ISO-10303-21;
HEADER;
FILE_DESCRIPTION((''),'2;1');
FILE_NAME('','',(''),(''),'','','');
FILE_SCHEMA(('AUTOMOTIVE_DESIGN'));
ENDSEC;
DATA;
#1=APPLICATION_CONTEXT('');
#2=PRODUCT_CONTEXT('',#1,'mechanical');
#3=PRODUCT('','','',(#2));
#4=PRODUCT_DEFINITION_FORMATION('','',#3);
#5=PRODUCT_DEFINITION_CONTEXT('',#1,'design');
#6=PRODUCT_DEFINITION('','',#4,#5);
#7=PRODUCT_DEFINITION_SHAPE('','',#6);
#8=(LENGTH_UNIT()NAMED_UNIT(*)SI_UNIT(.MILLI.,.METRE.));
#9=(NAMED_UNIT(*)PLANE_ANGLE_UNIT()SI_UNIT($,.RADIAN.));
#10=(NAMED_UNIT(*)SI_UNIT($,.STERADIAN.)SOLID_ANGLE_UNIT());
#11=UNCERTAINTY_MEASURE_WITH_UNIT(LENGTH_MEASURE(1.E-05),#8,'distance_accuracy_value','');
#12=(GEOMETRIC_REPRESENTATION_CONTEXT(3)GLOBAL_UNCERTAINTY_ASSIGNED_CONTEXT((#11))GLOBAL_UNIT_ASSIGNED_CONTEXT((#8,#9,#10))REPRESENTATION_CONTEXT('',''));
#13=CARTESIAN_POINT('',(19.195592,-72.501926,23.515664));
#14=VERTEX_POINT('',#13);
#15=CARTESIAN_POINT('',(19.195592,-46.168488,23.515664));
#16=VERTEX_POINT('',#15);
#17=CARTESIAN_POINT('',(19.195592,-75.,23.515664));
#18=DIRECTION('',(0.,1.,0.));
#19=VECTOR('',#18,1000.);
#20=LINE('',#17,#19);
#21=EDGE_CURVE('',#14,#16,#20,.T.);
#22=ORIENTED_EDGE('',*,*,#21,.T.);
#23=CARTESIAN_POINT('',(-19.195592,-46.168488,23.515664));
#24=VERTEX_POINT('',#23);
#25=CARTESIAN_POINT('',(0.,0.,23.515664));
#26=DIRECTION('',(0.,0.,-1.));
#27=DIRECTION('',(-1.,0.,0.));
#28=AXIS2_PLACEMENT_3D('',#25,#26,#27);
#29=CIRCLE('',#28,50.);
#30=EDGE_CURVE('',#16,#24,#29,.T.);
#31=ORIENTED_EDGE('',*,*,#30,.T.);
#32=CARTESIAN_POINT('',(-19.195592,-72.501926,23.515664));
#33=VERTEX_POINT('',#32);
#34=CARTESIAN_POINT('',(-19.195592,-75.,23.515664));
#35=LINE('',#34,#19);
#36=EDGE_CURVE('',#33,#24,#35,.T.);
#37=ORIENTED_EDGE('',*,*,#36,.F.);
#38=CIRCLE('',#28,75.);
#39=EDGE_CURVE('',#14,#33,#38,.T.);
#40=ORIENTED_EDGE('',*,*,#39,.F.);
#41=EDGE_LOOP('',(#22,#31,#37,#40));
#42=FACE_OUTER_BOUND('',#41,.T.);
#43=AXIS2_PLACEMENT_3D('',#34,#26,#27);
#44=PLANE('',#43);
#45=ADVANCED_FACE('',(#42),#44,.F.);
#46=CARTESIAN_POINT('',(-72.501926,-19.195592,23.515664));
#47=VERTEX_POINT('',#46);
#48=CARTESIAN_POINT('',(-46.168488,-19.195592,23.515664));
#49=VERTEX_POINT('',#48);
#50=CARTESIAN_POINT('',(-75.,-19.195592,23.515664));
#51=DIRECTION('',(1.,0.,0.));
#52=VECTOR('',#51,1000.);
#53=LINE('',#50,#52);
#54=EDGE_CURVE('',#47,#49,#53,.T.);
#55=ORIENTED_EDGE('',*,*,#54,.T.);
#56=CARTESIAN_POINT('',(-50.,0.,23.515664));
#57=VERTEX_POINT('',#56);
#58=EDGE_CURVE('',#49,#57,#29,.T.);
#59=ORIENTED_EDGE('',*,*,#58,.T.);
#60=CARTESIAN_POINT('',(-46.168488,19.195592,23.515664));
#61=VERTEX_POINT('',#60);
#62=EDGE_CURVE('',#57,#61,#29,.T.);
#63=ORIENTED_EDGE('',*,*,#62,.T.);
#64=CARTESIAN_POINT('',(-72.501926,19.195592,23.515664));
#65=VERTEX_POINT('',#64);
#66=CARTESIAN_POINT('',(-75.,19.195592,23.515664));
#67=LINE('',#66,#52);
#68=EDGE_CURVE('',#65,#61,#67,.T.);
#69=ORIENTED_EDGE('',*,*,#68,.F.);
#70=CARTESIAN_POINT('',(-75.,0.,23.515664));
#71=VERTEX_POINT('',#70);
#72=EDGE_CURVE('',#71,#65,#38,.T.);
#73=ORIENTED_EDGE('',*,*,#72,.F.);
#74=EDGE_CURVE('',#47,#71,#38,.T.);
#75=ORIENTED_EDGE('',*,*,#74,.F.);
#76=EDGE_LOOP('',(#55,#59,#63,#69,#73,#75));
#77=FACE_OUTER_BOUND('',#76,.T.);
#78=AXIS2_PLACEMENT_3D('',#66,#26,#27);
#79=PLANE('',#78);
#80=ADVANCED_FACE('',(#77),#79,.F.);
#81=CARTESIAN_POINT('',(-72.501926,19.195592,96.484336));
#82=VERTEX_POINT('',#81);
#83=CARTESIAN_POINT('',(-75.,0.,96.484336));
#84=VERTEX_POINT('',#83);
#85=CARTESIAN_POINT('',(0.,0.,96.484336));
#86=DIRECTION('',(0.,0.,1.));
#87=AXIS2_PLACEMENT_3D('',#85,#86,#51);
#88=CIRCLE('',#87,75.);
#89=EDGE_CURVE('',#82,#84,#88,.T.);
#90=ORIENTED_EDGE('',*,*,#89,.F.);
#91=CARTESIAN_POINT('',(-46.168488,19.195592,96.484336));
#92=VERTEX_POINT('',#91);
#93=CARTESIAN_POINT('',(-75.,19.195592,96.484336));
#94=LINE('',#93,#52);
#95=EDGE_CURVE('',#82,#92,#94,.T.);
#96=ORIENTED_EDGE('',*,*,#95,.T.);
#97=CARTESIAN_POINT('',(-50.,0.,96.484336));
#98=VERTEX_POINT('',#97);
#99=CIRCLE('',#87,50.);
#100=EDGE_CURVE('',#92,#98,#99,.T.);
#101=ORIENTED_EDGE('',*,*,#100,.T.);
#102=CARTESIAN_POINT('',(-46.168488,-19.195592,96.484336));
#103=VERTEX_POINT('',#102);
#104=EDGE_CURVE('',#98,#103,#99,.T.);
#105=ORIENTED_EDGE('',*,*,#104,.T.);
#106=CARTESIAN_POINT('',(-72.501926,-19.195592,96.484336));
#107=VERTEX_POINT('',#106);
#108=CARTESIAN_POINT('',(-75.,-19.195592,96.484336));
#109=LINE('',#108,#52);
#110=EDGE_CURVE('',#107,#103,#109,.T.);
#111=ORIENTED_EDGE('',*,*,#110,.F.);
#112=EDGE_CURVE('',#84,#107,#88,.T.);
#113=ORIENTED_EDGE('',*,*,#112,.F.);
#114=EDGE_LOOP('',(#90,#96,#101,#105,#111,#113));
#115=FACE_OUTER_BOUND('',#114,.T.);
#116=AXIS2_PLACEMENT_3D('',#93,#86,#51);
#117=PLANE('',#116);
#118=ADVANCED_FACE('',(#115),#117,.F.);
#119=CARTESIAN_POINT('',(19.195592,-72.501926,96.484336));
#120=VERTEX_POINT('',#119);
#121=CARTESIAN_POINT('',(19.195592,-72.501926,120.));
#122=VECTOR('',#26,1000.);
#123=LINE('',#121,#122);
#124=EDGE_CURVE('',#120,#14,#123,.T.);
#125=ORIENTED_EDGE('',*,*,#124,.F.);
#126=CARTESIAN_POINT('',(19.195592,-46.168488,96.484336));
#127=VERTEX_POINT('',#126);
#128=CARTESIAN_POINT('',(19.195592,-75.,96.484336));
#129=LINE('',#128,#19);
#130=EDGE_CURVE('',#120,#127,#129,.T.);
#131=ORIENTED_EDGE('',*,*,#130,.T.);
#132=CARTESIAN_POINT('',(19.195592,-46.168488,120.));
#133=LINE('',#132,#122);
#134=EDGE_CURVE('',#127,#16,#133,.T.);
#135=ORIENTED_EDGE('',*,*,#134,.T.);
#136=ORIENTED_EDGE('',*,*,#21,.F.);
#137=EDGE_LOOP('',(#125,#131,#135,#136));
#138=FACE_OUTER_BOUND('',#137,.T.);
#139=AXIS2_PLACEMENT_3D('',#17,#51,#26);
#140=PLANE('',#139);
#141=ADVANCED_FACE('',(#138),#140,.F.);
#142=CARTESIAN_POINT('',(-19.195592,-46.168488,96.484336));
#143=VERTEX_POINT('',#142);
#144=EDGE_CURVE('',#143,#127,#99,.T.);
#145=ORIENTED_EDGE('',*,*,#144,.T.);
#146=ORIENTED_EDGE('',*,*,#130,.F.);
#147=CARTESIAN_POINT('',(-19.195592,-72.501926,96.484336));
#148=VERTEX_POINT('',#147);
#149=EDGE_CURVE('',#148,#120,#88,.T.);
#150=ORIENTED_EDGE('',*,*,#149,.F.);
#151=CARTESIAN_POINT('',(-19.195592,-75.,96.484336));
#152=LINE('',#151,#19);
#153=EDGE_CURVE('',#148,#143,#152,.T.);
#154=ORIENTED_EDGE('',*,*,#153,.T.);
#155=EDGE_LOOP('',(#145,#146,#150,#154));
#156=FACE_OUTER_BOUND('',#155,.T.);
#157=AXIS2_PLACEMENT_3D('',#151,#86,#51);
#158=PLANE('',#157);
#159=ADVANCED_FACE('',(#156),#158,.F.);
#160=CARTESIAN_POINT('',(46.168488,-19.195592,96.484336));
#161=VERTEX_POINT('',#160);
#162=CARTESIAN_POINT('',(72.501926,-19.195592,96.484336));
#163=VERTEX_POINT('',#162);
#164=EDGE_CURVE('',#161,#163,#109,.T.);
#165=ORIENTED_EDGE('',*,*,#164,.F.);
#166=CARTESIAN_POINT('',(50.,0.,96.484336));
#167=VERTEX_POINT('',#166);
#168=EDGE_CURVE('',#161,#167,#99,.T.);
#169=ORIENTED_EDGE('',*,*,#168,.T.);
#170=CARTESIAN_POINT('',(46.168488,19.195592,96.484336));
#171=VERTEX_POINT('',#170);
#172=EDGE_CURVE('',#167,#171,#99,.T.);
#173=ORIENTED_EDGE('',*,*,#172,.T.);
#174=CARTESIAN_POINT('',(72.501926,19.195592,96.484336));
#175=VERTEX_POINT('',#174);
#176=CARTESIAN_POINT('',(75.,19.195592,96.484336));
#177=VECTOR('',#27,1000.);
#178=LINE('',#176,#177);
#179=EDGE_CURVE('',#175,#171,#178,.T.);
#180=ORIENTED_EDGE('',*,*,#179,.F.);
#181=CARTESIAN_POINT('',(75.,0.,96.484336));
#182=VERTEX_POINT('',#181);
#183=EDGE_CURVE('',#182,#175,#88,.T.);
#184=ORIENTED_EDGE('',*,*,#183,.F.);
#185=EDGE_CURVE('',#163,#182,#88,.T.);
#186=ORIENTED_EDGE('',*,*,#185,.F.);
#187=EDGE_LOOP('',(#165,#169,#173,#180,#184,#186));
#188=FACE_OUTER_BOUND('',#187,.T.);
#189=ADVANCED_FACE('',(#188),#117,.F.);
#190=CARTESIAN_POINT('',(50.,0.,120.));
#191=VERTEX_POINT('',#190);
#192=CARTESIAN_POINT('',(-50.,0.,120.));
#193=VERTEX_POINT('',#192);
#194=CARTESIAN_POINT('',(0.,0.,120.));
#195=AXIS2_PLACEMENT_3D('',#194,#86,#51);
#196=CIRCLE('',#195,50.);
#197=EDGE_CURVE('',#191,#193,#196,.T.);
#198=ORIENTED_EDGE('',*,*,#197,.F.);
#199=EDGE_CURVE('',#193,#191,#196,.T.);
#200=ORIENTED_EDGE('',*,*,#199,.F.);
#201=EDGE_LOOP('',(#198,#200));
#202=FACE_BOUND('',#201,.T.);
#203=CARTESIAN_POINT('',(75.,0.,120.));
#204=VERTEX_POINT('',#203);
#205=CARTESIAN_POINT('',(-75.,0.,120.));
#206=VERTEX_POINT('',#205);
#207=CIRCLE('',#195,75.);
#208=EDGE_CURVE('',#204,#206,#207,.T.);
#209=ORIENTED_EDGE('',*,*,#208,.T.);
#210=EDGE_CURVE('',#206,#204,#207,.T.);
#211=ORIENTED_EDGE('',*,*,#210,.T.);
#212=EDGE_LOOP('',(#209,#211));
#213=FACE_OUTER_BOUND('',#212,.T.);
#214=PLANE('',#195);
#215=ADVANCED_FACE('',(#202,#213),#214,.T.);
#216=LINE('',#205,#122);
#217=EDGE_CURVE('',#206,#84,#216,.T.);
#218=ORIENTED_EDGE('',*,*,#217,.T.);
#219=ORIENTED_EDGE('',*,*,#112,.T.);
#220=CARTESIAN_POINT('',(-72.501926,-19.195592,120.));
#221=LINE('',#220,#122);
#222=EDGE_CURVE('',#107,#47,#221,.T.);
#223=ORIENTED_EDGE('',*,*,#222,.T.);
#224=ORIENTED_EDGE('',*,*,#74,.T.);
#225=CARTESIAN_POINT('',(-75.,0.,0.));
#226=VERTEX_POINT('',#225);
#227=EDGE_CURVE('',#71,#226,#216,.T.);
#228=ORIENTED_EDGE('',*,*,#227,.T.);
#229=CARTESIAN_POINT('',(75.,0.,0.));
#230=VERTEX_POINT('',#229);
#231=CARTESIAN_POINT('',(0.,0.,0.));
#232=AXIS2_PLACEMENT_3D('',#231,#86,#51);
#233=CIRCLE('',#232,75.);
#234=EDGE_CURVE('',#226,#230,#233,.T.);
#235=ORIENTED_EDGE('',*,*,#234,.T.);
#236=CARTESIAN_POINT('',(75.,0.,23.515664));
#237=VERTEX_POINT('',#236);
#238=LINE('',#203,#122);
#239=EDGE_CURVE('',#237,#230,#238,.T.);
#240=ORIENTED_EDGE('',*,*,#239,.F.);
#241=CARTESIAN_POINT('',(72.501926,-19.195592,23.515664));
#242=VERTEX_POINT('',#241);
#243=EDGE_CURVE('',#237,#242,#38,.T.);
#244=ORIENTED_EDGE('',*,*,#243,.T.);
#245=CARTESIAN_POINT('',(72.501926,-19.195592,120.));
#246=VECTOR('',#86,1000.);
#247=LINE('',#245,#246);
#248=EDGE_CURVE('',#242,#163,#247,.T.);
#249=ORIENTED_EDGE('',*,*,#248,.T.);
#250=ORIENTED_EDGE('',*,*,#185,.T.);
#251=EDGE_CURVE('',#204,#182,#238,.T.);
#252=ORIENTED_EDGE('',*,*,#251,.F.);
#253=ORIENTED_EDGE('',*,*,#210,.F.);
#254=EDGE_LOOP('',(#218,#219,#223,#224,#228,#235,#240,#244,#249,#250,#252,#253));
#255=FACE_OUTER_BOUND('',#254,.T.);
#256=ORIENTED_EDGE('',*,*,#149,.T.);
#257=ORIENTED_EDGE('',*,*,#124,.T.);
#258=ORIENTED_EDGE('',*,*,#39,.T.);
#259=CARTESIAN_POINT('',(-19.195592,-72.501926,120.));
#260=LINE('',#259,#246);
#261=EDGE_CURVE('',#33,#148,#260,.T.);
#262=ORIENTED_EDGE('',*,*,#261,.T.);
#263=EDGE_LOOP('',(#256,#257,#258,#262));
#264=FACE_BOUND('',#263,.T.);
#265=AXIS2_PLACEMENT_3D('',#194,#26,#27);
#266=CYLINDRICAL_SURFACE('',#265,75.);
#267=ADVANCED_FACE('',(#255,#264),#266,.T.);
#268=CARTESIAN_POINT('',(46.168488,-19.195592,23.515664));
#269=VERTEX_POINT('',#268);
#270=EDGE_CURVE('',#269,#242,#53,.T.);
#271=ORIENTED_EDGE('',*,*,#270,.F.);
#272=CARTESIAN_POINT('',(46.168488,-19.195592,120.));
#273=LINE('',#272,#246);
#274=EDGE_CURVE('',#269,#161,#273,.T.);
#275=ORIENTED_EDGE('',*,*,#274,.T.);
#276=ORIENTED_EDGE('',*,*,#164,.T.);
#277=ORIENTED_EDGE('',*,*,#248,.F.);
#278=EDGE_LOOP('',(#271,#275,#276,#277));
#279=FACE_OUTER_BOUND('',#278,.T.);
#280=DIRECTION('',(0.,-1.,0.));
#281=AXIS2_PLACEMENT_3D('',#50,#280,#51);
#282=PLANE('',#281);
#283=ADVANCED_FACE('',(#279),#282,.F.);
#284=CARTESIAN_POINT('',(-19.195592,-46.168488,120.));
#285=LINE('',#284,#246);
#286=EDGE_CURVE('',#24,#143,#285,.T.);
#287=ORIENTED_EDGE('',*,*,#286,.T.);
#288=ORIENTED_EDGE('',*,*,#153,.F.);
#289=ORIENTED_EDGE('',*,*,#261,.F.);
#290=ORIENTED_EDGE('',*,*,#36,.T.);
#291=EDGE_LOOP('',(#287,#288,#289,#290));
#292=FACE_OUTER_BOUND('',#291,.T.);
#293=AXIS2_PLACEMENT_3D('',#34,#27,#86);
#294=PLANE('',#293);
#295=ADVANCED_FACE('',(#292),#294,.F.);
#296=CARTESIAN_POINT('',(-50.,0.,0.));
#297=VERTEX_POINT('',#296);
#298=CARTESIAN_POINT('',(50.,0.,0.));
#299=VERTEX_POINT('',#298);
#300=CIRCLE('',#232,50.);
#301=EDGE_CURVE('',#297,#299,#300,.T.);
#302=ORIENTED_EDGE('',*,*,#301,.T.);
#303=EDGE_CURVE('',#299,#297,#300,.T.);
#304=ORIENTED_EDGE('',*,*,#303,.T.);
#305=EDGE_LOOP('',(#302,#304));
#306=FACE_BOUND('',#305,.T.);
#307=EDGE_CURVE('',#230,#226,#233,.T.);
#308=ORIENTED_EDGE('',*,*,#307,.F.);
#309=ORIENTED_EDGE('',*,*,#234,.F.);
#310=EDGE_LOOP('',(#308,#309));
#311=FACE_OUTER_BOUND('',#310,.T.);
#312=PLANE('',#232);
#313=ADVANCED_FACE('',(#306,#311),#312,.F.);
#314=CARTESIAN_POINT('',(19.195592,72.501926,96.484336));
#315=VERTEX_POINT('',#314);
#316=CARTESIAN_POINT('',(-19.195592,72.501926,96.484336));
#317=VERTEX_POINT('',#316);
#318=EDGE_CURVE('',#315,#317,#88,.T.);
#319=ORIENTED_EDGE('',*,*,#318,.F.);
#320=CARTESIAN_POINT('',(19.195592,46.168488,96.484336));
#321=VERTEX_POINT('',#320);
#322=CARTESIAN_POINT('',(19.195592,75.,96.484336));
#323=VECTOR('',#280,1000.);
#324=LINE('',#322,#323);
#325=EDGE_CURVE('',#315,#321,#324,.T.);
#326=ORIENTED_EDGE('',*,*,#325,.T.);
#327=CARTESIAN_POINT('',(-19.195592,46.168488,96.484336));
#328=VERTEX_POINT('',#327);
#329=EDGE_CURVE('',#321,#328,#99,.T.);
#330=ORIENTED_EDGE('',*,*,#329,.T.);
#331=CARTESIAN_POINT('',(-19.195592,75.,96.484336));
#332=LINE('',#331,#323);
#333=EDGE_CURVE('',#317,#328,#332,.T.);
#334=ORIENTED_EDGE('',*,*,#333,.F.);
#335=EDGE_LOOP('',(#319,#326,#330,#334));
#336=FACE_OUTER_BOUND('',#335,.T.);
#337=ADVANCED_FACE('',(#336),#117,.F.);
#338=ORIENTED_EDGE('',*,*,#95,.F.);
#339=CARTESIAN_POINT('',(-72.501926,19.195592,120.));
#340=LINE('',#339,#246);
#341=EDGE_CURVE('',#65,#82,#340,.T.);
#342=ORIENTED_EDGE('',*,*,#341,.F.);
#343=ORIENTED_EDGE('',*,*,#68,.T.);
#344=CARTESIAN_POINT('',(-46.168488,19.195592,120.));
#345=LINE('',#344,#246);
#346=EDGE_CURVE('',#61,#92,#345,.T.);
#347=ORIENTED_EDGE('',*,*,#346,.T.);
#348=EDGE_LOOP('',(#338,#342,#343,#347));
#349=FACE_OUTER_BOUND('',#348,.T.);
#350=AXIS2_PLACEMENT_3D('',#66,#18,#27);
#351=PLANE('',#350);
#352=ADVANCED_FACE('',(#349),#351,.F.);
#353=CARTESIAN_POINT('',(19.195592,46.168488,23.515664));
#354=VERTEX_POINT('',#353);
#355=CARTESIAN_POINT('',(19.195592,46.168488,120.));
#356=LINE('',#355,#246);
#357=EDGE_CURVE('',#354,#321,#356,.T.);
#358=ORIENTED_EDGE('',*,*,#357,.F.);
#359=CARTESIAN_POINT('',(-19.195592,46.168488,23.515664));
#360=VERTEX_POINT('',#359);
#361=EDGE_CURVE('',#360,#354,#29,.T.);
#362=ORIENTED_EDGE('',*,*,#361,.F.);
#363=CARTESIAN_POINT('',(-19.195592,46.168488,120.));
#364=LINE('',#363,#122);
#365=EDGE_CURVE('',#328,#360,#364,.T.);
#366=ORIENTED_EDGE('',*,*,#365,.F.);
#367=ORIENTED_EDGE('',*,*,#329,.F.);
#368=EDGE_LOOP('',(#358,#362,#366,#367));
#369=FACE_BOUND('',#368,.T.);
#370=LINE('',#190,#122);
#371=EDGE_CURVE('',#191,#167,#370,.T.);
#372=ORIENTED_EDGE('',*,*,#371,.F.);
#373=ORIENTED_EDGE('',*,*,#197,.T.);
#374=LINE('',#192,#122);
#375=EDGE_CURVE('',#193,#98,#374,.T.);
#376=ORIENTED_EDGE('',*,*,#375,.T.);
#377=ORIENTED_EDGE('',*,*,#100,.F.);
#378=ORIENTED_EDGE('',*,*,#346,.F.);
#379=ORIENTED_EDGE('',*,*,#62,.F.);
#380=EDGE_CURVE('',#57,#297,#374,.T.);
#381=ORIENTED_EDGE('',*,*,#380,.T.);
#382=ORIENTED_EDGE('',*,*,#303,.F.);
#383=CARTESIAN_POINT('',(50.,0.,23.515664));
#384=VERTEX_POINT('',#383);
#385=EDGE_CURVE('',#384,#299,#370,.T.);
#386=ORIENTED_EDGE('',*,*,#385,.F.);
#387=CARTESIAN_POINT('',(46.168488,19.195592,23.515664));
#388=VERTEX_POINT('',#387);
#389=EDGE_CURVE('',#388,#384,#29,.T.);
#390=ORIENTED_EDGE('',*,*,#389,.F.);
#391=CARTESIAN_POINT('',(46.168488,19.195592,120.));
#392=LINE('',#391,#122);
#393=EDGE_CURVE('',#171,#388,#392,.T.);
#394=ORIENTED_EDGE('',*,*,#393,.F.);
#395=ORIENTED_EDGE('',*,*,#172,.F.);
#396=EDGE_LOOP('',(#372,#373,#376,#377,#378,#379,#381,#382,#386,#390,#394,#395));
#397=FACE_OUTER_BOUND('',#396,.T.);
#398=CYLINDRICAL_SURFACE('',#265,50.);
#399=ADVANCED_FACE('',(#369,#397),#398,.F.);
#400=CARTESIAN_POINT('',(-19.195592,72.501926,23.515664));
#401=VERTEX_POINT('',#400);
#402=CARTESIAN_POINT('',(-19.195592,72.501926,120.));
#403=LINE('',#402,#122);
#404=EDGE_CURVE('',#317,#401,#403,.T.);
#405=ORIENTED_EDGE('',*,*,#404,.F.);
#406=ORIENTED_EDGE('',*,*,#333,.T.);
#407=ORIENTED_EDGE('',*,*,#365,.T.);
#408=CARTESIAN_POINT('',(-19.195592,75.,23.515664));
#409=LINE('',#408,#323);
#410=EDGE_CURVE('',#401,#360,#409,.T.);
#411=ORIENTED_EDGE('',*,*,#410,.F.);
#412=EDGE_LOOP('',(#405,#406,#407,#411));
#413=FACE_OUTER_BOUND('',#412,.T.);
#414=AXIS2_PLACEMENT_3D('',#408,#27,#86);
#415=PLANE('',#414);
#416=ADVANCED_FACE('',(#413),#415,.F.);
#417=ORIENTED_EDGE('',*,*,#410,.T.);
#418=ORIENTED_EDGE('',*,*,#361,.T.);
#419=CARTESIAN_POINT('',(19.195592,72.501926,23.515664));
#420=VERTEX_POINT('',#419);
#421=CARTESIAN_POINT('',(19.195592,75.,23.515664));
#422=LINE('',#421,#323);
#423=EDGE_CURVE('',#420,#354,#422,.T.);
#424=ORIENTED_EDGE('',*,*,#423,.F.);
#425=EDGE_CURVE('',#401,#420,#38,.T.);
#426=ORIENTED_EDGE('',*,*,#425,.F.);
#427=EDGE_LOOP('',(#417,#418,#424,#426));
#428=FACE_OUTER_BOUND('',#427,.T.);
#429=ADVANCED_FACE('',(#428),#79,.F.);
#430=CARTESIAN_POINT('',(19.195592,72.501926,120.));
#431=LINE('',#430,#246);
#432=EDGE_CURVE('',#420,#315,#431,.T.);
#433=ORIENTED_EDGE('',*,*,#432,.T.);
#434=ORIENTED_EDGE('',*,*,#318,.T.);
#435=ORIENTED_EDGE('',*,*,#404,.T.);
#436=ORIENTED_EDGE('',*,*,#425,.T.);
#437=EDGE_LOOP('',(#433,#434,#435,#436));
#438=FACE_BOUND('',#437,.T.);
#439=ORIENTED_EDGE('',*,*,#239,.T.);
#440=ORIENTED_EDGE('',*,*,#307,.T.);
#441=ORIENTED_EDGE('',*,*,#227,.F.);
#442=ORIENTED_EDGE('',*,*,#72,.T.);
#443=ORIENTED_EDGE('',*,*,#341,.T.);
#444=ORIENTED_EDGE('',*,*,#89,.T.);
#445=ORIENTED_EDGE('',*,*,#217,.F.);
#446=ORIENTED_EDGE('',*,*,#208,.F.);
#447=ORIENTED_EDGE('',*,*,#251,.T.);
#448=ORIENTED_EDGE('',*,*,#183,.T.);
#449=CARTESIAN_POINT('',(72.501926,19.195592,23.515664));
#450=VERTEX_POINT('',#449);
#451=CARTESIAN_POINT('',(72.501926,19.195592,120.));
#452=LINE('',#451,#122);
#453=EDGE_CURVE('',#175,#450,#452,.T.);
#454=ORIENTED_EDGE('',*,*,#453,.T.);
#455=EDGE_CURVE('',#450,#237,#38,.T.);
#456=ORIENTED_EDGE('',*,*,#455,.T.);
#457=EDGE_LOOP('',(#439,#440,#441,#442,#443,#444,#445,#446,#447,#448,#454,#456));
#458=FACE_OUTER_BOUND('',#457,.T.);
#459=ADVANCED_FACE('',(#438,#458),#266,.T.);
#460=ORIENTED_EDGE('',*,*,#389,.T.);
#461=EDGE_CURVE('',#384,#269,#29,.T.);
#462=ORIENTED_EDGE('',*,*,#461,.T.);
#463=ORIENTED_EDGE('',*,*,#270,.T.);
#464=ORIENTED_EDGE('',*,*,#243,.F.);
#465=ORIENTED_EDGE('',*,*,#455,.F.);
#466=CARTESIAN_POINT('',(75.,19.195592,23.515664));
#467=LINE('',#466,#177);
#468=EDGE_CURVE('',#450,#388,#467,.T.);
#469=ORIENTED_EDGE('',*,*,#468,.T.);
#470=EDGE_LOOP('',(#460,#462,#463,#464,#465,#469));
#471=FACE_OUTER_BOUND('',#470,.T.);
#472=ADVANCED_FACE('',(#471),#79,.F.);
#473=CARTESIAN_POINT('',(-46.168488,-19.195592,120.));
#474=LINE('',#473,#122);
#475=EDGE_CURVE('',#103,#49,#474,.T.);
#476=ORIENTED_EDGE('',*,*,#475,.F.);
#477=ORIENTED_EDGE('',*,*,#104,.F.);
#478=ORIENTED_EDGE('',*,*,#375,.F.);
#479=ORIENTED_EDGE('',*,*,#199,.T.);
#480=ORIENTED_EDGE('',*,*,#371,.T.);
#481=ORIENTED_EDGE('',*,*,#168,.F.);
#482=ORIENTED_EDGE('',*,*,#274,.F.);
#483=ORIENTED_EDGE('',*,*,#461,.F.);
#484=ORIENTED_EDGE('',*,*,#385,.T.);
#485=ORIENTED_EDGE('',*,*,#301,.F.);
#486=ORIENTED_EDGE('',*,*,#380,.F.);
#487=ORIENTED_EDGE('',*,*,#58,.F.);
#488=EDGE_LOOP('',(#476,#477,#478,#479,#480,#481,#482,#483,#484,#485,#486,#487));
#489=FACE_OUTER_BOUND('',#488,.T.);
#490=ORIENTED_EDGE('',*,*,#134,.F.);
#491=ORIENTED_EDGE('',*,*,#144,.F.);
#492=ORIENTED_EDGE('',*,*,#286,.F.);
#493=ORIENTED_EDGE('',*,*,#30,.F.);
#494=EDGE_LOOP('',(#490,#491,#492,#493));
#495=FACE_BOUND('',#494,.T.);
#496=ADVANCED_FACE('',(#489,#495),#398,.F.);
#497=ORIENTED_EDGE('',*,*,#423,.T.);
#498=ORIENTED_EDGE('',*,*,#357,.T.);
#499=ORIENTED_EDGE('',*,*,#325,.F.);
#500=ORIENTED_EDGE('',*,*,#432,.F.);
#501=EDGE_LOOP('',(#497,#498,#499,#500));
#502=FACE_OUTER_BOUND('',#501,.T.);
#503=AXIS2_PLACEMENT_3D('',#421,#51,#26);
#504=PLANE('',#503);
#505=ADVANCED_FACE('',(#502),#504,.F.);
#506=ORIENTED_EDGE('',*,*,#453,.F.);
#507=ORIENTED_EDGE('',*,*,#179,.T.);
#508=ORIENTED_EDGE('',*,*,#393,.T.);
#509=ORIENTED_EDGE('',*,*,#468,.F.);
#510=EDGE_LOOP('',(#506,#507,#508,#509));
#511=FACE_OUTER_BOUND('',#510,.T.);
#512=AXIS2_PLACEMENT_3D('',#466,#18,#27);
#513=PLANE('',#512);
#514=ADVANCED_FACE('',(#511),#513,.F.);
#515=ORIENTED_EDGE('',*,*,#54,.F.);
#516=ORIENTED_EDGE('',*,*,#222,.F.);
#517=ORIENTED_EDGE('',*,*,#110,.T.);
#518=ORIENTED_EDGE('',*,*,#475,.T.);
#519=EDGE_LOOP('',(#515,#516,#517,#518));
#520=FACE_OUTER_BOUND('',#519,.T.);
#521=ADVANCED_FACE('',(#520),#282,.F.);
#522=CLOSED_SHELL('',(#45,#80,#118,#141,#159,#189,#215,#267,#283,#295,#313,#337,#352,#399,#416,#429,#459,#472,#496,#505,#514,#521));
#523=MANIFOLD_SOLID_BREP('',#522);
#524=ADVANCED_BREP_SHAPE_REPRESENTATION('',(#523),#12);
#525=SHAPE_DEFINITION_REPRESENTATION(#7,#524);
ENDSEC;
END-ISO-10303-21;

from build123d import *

# Parameters (mm, degrees)
SKETCH1_R           = 75
SKETCH1_R_2         = 50
BOSS_EXTRUDE1_DEPTH = 120
SKETCH2_W           = 38.391183042
SKETCH2_H           = 72.968672404
CUT_EXTRUDE1_DEPTH  = 161.15617378
CIRPATTERN1_COUNT   = 4


with BuildPart() as part:
    # Sketch1 → Boss-Extrude1 (new body)
    with BuildSketch(Plane.XY):
        Circle(SKETCH1_R)
        Circle(SKETCH1_R_2, mode=Mode.SUBTRACT)
    extrude(amount=BOSS_EXTRUDE1_DEPTH)

    # Sketch2 → Cut-Extrude1 (cut, through all)
    with BuildSketch(Plane(origin=(0, 0, 0), x_dir=(1, 0, 0), z_dir=(0, 1, 0))):
        with Locations((0, -60)):
            Rectangle(SKETCH2_W, SKETCH2_H)
    cut_extrude1 = extrude(amount=-CUT_EXTRUDE1_DEPTH, mode=Mode.SUBTRACT)

    # CirPattern1: Cut-Extrude1 ×4 about axis
    cirpattern1_axis = Axis((0, 0, 0), (0, 0, 1))
    for i in range(1, CIRPATTERN1_COUNT):
        add(cut_extrude1.rotate(cirpattern1_axis, i * 360 / CIRPATTERN1_COUNT), mode=Mode.SUBTRACT)


solid = part.part
